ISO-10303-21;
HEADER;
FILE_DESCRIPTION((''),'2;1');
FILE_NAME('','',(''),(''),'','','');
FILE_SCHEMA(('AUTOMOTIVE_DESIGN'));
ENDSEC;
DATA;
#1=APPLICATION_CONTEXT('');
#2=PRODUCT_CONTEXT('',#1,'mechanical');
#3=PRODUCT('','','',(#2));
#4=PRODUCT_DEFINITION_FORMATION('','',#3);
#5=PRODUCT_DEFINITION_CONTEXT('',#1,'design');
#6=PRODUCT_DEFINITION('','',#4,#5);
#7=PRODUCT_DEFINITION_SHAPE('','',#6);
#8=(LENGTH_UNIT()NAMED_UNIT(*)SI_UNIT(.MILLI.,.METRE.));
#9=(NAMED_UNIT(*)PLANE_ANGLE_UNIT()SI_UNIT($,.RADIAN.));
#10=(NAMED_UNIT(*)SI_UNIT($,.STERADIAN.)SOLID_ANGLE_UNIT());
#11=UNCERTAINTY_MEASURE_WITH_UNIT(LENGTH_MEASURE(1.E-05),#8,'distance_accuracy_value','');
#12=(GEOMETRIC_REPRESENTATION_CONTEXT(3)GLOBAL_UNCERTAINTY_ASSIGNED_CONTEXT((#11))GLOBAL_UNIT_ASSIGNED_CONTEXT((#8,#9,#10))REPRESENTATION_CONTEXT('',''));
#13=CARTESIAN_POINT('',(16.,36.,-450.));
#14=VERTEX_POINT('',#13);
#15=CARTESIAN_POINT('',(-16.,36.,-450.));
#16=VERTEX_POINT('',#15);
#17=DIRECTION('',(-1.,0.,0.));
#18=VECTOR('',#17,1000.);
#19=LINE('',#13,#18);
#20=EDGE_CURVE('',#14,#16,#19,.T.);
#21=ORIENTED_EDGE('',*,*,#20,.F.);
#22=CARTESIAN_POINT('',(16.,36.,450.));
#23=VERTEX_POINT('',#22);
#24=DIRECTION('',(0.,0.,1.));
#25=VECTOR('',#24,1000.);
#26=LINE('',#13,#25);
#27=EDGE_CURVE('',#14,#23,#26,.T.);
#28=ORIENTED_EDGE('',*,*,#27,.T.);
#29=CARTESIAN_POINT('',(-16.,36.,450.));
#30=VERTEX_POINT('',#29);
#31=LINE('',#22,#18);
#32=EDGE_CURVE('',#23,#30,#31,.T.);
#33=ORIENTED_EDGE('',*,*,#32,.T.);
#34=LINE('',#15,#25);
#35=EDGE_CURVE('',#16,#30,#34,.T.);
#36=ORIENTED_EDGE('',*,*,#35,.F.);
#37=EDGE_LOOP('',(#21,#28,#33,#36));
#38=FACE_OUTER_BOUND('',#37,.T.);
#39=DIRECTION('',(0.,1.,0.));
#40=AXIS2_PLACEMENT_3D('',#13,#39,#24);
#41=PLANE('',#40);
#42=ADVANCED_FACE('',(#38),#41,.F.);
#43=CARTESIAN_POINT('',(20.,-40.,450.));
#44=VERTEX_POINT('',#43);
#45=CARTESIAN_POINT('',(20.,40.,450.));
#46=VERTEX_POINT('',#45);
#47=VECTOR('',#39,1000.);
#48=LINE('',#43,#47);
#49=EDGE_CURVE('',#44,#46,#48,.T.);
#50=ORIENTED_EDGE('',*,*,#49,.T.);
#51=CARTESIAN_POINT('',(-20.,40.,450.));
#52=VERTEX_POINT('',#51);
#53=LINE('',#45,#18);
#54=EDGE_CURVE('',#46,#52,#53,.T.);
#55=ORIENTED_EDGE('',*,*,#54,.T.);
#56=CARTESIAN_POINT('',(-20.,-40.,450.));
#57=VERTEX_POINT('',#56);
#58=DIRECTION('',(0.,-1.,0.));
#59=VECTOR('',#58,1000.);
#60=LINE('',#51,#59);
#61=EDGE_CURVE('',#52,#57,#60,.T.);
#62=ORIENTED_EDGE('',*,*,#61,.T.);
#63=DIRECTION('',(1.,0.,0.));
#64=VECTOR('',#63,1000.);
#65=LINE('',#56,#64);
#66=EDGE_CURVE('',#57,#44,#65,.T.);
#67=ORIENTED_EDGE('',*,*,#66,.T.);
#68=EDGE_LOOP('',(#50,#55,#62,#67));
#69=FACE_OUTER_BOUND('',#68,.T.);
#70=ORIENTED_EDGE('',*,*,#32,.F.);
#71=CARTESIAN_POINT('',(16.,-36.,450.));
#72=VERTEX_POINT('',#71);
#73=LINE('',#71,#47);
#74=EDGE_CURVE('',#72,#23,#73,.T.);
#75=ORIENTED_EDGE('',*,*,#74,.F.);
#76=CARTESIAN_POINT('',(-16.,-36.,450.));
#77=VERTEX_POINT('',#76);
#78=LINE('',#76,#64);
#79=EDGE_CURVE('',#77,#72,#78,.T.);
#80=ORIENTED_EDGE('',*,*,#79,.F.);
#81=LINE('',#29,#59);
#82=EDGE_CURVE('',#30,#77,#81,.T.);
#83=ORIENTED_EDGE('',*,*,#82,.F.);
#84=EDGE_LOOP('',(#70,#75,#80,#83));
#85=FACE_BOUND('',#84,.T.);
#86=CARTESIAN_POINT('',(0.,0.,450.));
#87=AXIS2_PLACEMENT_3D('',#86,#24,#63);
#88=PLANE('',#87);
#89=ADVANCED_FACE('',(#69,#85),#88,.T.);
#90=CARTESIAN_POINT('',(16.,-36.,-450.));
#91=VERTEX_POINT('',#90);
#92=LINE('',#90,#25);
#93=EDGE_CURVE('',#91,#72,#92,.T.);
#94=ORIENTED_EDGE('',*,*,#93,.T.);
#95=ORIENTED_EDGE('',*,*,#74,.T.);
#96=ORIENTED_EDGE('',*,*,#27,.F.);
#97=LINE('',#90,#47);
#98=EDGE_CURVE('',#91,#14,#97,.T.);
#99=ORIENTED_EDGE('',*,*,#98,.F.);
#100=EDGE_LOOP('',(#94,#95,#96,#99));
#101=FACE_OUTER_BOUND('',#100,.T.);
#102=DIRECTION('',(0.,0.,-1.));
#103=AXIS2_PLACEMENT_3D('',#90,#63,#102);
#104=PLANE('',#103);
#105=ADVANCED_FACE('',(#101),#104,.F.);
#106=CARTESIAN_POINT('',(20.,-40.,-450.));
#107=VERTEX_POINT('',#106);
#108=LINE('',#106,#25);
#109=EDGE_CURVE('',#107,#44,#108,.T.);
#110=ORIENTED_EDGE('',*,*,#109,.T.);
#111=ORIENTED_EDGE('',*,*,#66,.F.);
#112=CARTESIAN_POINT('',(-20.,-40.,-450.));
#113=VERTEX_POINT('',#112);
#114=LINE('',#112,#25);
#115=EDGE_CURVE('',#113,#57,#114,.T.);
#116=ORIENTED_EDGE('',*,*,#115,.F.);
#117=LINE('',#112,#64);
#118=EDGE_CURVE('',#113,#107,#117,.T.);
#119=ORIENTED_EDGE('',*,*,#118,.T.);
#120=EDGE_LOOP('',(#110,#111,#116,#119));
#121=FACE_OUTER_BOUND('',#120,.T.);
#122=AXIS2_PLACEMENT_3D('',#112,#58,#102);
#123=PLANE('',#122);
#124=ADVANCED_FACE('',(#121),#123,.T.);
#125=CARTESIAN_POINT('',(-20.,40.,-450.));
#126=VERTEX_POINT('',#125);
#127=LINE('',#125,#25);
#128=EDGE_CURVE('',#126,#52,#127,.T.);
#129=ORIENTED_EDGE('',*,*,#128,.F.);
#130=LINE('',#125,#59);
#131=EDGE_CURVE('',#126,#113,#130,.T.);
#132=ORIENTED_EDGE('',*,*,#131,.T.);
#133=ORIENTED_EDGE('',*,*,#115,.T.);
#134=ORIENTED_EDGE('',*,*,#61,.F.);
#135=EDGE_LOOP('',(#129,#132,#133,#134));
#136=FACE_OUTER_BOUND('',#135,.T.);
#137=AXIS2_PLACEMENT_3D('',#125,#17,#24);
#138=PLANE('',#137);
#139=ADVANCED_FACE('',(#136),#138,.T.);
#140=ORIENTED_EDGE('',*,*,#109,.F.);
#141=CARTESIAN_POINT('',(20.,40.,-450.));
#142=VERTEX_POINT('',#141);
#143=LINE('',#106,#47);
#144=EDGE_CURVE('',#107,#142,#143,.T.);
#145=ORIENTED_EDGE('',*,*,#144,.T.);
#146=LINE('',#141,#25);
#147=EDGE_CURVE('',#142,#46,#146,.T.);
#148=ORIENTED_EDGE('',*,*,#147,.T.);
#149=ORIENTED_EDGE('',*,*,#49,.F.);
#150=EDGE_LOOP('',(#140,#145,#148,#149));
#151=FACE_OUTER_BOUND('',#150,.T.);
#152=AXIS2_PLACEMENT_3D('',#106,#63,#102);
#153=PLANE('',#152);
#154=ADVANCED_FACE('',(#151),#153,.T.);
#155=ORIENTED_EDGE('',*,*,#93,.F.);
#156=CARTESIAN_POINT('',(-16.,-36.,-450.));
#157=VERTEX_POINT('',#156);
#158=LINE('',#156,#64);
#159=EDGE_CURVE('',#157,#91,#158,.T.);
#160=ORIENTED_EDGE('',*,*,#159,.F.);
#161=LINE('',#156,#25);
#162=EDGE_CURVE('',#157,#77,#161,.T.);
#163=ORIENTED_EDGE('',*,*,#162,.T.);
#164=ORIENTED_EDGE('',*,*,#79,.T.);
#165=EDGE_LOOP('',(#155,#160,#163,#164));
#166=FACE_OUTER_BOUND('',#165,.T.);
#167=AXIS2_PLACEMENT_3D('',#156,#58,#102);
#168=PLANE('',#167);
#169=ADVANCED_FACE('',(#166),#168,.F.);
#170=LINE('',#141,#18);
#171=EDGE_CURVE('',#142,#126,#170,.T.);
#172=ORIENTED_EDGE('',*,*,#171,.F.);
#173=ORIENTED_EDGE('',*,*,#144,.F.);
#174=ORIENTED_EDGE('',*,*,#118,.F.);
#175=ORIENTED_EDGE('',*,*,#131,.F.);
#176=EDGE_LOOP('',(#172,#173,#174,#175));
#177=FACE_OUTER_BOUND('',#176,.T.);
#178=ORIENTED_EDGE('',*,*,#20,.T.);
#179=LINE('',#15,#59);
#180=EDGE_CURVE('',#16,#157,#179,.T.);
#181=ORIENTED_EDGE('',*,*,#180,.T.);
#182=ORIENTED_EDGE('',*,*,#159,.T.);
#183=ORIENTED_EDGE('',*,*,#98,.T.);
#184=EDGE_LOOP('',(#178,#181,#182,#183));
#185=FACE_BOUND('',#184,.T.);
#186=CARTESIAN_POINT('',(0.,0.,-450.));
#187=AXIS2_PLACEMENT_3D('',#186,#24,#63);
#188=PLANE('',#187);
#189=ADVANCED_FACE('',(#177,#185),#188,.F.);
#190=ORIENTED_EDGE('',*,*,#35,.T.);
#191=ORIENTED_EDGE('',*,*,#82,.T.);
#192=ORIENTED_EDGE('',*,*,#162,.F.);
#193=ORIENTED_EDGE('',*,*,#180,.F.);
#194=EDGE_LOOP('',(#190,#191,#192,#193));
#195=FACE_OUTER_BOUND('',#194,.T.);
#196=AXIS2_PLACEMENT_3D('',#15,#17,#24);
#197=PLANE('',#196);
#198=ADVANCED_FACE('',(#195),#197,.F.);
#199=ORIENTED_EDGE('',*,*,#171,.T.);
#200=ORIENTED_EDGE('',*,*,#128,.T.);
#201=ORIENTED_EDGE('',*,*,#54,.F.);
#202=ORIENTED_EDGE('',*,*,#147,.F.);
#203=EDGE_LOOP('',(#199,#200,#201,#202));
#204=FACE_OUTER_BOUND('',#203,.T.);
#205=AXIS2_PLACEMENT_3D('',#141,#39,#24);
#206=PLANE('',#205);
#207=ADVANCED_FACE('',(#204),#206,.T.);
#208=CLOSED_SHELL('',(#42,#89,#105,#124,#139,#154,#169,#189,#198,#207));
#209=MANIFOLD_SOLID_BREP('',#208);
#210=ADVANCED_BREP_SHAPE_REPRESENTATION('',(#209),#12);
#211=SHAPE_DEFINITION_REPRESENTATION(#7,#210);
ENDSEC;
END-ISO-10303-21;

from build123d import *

# Parameters (mm, degrees)
SKETCH_1_W      = 40
SKETCH_1_H      = 80
SKETCH_1_W_2    = 32
SKETCH_1_H_2    = 72
EXTRUDE_1_DEPTH = 450


with BuildPart() as part:
    # 草图1 → 凸台-拉伸1 (new, symmetric)
    with BuildSketch(Plane.XY):
        Rectangle(SKETCH_1_W, SKETCH_1_H)
        Rectangle(SKETCH_1_W_2, SKETCH_1_H_2, mode=Mode.SUBTRACT)
    extrude(amount=EXTRUDE_1_DEPTH, both=True)


solid = part.part
